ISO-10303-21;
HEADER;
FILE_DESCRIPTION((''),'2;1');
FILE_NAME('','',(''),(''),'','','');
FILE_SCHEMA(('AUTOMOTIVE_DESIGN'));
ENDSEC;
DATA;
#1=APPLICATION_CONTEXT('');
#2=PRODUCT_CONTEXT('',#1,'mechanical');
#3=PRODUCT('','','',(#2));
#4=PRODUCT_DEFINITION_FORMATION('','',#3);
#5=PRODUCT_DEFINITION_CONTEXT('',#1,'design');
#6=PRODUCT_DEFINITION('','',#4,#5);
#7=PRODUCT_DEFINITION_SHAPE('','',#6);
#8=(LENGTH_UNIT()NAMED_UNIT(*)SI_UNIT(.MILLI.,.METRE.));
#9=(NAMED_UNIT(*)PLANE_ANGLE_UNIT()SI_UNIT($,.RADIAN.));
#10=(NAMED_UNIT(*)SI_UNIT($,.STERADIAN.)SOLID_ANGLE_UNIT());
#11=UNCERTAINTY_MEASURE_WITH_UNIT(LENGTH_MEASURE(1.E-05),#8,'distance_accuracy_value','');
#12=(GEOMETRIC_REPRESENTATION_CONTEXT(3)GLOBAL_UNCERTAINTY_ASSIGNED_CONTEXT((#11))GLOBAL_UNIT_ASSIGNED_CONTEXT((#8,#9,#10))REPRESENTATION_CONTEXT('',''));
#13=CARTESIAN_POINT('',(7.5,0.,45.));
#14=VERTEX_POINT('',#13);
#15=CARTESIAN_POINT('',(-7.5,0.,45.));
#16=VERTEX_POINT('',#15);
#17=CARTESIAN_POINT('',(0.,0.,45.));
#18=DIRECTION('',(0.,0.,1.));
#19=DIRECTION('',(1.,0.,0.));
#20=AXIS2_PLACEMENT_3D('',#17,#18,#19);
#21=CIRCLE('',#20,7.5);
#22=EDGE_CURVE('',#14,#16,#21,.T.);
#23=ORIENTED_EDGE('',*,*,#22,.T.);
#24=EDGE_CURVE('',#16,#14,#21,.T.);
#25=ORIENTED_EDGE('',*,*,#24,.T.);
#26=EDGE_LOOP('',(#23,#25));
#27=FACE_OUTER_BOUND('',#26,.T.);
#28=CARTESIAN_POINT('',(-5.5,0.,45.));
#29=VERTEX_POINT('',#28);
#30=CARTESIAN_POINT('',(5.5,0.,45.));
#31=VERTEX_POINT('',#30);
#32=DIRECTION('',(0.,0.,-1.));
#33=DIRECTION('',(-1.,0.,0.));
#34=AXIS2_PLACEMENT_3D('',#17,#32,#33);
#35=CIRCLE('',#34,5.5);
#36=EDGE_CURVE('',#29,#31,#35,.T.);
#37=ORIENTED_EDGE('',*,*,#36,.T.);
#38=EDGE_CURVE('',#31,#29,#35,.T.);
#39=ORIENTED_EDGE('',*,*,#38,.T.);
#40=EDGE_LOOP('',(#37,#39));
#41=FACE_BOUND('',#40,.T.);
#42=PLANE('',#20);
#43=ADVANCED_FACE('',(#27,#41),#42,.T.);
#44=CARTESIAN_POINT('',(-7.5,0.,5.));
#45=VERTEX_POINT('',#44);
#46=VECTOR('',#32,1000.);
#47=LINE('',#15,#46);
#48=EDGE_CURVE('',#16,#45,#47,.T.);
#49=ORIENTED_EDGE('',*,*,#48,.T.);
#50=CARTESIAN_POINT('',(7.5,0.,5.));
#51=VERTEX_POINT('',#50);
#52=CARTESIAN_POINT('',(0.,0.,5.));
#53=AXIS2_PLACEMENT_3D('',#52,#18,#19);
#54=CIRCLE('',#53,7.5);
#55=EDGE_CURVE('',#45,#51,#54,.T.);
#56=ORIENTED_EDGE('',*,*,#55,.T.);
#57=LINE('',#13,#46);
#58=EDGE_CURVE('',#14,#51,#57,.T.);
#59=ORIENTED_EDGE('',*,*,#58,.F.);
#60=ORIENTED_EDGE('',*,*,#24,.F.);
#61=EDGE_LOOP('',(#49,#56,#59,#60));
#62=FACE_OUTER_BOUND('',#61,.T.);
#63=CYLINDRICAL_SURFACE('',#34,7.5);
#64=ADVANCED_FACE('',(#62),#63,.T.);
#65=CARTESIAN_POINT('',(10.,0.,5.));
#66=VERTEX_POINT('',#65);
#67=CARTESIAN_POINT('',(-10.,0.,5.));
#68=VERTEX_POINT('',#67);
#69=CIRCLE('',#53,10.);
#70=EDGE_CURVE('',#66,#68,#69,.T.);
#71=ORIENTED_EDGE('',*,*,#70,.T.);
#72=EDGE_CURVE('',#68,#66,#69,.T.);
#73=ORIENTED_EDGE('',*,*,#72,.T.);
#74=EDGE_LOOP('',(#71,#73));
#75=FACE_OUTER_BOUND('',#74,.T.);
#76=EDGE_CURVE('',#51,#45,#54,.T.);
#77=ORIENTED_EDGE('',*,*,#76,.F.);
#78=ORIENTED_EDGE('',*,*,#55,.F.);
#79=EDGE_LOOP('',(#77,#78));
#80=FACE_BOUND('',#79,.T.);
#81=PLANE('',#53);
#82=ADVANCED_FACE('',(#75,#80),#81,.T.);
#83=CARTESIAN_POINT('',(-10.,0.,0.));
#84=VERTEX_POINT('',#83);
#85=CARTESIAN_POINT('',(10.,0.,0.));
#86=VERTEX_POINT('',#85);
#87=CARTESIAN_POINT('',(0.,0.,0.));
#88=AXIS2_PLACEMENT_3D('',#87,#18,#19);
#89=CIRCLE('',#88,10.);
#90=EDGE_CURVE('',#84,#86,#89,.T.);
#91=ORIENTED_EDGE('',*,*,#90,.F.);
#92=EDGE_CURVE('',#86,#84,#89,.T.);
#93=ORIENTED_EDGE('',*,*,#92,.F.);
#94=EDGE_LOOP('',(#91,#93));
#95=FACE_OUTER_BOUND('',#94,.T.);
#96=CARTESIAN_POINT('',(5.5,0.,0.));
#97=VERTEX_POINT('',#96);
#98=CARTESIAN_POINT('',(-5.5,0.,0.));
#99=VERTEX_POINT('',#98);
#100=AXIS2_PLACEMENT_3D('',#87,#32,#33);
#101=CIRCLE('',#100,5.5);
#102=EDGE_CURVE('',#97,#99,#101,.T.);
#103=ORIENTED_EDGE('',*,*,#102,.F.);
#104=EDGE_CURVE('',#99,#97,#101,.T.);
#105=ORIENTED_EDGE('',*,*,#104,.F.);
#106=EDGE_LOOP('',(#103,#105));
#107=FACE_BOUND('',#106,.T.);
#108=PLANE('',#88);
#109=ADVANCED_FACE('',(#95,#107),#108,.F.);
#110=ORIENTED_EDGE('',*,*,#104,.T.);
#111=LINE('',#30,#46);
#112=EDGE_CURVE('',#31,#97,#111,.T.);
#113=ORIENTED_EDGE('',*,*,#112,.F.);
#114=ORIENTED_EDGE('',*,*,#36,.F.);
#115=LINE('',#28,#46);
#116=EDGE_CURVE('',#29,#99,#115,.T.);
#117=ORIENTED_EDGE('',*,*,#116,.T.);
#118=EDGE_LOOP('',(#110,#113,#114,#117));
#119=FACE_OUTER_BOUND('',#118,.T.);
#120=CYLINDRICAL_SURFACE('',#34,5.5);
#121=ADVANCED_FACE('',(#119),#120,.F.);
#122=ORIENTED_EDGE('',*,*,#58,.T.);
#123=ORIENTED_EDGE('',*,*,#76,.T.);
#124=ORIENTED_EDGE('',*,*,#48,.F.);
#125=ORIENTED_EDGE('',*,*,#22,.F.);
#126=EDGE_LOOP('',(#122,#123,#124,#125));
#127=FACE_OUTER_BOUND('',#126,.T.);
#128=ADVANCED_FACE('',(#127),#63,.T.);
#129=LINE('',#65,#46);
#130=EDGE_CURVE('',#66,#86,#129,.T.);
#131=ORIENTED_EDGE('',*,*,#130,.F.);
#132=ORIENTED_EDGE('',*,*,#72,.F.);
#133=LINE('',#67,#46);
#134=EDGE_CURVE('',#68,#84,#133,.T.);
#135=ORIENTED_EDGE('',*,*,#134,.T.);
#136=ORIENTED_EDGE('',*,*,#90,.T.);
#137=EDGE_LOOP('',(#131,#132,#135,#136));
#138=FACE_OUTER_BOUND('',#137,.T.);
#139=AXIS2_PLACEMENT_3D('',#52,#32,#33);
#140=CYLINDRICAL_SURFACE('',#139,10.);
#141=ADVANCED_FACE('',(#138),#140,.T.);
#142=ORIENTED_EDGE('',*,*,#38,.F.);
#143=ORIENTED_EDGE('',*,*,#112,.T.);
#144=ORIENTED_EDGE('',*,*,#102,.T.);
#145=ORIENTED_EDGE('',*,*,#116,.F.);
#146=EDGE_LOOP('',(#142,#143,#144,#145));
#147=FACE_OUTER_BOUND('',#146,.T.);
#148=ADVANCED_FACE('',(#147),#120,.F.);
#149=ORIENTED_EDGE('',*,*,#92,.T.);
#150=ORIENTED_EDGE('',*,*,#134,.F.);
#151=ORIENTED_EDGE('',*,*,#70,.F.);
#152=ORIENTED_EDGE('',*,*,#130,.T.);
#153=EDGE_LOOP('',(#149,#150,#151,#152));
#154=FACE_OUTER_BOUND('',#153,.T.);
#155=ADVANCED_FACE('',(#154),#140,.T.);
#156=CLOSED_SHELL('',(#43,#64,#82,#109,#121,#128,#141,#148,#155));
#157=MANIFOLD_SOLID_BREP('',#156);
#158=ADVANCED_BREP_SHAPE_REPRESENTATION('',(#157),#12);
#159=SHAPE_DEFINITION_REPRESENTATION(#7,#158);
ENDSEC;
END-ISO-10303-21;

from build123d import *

# Parameters (mm, degrees)
FLANGE_PROFILE_20_R   = 10
FLANGE_20X5_DEPTH     = 5
SHANK_PROFILE_15_R    = 7.5
SHANK_15X40_DEPTH     = 40
BORE_PROFILE_11_R     = 5.5
BORE_11_THROUGH_DEPTH = 48.16990566


with BuildPart() as part:
    # Flange Profile Ø20 → Flange Ø20x5 (new body)
    with BuildSketch(Plane.XY):
        Circle(FLANGE_PROFILE_20_R)
    extrude(amount=FLANGE_20X5_DEPTH)

    # Shank Profile Ø15 → Shank Ø15x40 (add)
    with BuildSketch(Plane.XY.offset(5)):
        Circle(SHANK_PROFILE_15_R)
    extrude(amount=SHANK_15X40_DEPTH)

    # Bore Profile Ø11 → Bore Ø11 Through (cut, through all)
    with BuildSketch(Plane(origin=(0, 0, 0), x_dir=(-1, 0, 0), z_dir=(0, 0, -1))):
        Circle(BORE_PROFILE_11_R)
    extrude(amount=-BORE_11_THROUGH_DEPTH, mode=Mode.SUBTRACT)


solid = part.part
